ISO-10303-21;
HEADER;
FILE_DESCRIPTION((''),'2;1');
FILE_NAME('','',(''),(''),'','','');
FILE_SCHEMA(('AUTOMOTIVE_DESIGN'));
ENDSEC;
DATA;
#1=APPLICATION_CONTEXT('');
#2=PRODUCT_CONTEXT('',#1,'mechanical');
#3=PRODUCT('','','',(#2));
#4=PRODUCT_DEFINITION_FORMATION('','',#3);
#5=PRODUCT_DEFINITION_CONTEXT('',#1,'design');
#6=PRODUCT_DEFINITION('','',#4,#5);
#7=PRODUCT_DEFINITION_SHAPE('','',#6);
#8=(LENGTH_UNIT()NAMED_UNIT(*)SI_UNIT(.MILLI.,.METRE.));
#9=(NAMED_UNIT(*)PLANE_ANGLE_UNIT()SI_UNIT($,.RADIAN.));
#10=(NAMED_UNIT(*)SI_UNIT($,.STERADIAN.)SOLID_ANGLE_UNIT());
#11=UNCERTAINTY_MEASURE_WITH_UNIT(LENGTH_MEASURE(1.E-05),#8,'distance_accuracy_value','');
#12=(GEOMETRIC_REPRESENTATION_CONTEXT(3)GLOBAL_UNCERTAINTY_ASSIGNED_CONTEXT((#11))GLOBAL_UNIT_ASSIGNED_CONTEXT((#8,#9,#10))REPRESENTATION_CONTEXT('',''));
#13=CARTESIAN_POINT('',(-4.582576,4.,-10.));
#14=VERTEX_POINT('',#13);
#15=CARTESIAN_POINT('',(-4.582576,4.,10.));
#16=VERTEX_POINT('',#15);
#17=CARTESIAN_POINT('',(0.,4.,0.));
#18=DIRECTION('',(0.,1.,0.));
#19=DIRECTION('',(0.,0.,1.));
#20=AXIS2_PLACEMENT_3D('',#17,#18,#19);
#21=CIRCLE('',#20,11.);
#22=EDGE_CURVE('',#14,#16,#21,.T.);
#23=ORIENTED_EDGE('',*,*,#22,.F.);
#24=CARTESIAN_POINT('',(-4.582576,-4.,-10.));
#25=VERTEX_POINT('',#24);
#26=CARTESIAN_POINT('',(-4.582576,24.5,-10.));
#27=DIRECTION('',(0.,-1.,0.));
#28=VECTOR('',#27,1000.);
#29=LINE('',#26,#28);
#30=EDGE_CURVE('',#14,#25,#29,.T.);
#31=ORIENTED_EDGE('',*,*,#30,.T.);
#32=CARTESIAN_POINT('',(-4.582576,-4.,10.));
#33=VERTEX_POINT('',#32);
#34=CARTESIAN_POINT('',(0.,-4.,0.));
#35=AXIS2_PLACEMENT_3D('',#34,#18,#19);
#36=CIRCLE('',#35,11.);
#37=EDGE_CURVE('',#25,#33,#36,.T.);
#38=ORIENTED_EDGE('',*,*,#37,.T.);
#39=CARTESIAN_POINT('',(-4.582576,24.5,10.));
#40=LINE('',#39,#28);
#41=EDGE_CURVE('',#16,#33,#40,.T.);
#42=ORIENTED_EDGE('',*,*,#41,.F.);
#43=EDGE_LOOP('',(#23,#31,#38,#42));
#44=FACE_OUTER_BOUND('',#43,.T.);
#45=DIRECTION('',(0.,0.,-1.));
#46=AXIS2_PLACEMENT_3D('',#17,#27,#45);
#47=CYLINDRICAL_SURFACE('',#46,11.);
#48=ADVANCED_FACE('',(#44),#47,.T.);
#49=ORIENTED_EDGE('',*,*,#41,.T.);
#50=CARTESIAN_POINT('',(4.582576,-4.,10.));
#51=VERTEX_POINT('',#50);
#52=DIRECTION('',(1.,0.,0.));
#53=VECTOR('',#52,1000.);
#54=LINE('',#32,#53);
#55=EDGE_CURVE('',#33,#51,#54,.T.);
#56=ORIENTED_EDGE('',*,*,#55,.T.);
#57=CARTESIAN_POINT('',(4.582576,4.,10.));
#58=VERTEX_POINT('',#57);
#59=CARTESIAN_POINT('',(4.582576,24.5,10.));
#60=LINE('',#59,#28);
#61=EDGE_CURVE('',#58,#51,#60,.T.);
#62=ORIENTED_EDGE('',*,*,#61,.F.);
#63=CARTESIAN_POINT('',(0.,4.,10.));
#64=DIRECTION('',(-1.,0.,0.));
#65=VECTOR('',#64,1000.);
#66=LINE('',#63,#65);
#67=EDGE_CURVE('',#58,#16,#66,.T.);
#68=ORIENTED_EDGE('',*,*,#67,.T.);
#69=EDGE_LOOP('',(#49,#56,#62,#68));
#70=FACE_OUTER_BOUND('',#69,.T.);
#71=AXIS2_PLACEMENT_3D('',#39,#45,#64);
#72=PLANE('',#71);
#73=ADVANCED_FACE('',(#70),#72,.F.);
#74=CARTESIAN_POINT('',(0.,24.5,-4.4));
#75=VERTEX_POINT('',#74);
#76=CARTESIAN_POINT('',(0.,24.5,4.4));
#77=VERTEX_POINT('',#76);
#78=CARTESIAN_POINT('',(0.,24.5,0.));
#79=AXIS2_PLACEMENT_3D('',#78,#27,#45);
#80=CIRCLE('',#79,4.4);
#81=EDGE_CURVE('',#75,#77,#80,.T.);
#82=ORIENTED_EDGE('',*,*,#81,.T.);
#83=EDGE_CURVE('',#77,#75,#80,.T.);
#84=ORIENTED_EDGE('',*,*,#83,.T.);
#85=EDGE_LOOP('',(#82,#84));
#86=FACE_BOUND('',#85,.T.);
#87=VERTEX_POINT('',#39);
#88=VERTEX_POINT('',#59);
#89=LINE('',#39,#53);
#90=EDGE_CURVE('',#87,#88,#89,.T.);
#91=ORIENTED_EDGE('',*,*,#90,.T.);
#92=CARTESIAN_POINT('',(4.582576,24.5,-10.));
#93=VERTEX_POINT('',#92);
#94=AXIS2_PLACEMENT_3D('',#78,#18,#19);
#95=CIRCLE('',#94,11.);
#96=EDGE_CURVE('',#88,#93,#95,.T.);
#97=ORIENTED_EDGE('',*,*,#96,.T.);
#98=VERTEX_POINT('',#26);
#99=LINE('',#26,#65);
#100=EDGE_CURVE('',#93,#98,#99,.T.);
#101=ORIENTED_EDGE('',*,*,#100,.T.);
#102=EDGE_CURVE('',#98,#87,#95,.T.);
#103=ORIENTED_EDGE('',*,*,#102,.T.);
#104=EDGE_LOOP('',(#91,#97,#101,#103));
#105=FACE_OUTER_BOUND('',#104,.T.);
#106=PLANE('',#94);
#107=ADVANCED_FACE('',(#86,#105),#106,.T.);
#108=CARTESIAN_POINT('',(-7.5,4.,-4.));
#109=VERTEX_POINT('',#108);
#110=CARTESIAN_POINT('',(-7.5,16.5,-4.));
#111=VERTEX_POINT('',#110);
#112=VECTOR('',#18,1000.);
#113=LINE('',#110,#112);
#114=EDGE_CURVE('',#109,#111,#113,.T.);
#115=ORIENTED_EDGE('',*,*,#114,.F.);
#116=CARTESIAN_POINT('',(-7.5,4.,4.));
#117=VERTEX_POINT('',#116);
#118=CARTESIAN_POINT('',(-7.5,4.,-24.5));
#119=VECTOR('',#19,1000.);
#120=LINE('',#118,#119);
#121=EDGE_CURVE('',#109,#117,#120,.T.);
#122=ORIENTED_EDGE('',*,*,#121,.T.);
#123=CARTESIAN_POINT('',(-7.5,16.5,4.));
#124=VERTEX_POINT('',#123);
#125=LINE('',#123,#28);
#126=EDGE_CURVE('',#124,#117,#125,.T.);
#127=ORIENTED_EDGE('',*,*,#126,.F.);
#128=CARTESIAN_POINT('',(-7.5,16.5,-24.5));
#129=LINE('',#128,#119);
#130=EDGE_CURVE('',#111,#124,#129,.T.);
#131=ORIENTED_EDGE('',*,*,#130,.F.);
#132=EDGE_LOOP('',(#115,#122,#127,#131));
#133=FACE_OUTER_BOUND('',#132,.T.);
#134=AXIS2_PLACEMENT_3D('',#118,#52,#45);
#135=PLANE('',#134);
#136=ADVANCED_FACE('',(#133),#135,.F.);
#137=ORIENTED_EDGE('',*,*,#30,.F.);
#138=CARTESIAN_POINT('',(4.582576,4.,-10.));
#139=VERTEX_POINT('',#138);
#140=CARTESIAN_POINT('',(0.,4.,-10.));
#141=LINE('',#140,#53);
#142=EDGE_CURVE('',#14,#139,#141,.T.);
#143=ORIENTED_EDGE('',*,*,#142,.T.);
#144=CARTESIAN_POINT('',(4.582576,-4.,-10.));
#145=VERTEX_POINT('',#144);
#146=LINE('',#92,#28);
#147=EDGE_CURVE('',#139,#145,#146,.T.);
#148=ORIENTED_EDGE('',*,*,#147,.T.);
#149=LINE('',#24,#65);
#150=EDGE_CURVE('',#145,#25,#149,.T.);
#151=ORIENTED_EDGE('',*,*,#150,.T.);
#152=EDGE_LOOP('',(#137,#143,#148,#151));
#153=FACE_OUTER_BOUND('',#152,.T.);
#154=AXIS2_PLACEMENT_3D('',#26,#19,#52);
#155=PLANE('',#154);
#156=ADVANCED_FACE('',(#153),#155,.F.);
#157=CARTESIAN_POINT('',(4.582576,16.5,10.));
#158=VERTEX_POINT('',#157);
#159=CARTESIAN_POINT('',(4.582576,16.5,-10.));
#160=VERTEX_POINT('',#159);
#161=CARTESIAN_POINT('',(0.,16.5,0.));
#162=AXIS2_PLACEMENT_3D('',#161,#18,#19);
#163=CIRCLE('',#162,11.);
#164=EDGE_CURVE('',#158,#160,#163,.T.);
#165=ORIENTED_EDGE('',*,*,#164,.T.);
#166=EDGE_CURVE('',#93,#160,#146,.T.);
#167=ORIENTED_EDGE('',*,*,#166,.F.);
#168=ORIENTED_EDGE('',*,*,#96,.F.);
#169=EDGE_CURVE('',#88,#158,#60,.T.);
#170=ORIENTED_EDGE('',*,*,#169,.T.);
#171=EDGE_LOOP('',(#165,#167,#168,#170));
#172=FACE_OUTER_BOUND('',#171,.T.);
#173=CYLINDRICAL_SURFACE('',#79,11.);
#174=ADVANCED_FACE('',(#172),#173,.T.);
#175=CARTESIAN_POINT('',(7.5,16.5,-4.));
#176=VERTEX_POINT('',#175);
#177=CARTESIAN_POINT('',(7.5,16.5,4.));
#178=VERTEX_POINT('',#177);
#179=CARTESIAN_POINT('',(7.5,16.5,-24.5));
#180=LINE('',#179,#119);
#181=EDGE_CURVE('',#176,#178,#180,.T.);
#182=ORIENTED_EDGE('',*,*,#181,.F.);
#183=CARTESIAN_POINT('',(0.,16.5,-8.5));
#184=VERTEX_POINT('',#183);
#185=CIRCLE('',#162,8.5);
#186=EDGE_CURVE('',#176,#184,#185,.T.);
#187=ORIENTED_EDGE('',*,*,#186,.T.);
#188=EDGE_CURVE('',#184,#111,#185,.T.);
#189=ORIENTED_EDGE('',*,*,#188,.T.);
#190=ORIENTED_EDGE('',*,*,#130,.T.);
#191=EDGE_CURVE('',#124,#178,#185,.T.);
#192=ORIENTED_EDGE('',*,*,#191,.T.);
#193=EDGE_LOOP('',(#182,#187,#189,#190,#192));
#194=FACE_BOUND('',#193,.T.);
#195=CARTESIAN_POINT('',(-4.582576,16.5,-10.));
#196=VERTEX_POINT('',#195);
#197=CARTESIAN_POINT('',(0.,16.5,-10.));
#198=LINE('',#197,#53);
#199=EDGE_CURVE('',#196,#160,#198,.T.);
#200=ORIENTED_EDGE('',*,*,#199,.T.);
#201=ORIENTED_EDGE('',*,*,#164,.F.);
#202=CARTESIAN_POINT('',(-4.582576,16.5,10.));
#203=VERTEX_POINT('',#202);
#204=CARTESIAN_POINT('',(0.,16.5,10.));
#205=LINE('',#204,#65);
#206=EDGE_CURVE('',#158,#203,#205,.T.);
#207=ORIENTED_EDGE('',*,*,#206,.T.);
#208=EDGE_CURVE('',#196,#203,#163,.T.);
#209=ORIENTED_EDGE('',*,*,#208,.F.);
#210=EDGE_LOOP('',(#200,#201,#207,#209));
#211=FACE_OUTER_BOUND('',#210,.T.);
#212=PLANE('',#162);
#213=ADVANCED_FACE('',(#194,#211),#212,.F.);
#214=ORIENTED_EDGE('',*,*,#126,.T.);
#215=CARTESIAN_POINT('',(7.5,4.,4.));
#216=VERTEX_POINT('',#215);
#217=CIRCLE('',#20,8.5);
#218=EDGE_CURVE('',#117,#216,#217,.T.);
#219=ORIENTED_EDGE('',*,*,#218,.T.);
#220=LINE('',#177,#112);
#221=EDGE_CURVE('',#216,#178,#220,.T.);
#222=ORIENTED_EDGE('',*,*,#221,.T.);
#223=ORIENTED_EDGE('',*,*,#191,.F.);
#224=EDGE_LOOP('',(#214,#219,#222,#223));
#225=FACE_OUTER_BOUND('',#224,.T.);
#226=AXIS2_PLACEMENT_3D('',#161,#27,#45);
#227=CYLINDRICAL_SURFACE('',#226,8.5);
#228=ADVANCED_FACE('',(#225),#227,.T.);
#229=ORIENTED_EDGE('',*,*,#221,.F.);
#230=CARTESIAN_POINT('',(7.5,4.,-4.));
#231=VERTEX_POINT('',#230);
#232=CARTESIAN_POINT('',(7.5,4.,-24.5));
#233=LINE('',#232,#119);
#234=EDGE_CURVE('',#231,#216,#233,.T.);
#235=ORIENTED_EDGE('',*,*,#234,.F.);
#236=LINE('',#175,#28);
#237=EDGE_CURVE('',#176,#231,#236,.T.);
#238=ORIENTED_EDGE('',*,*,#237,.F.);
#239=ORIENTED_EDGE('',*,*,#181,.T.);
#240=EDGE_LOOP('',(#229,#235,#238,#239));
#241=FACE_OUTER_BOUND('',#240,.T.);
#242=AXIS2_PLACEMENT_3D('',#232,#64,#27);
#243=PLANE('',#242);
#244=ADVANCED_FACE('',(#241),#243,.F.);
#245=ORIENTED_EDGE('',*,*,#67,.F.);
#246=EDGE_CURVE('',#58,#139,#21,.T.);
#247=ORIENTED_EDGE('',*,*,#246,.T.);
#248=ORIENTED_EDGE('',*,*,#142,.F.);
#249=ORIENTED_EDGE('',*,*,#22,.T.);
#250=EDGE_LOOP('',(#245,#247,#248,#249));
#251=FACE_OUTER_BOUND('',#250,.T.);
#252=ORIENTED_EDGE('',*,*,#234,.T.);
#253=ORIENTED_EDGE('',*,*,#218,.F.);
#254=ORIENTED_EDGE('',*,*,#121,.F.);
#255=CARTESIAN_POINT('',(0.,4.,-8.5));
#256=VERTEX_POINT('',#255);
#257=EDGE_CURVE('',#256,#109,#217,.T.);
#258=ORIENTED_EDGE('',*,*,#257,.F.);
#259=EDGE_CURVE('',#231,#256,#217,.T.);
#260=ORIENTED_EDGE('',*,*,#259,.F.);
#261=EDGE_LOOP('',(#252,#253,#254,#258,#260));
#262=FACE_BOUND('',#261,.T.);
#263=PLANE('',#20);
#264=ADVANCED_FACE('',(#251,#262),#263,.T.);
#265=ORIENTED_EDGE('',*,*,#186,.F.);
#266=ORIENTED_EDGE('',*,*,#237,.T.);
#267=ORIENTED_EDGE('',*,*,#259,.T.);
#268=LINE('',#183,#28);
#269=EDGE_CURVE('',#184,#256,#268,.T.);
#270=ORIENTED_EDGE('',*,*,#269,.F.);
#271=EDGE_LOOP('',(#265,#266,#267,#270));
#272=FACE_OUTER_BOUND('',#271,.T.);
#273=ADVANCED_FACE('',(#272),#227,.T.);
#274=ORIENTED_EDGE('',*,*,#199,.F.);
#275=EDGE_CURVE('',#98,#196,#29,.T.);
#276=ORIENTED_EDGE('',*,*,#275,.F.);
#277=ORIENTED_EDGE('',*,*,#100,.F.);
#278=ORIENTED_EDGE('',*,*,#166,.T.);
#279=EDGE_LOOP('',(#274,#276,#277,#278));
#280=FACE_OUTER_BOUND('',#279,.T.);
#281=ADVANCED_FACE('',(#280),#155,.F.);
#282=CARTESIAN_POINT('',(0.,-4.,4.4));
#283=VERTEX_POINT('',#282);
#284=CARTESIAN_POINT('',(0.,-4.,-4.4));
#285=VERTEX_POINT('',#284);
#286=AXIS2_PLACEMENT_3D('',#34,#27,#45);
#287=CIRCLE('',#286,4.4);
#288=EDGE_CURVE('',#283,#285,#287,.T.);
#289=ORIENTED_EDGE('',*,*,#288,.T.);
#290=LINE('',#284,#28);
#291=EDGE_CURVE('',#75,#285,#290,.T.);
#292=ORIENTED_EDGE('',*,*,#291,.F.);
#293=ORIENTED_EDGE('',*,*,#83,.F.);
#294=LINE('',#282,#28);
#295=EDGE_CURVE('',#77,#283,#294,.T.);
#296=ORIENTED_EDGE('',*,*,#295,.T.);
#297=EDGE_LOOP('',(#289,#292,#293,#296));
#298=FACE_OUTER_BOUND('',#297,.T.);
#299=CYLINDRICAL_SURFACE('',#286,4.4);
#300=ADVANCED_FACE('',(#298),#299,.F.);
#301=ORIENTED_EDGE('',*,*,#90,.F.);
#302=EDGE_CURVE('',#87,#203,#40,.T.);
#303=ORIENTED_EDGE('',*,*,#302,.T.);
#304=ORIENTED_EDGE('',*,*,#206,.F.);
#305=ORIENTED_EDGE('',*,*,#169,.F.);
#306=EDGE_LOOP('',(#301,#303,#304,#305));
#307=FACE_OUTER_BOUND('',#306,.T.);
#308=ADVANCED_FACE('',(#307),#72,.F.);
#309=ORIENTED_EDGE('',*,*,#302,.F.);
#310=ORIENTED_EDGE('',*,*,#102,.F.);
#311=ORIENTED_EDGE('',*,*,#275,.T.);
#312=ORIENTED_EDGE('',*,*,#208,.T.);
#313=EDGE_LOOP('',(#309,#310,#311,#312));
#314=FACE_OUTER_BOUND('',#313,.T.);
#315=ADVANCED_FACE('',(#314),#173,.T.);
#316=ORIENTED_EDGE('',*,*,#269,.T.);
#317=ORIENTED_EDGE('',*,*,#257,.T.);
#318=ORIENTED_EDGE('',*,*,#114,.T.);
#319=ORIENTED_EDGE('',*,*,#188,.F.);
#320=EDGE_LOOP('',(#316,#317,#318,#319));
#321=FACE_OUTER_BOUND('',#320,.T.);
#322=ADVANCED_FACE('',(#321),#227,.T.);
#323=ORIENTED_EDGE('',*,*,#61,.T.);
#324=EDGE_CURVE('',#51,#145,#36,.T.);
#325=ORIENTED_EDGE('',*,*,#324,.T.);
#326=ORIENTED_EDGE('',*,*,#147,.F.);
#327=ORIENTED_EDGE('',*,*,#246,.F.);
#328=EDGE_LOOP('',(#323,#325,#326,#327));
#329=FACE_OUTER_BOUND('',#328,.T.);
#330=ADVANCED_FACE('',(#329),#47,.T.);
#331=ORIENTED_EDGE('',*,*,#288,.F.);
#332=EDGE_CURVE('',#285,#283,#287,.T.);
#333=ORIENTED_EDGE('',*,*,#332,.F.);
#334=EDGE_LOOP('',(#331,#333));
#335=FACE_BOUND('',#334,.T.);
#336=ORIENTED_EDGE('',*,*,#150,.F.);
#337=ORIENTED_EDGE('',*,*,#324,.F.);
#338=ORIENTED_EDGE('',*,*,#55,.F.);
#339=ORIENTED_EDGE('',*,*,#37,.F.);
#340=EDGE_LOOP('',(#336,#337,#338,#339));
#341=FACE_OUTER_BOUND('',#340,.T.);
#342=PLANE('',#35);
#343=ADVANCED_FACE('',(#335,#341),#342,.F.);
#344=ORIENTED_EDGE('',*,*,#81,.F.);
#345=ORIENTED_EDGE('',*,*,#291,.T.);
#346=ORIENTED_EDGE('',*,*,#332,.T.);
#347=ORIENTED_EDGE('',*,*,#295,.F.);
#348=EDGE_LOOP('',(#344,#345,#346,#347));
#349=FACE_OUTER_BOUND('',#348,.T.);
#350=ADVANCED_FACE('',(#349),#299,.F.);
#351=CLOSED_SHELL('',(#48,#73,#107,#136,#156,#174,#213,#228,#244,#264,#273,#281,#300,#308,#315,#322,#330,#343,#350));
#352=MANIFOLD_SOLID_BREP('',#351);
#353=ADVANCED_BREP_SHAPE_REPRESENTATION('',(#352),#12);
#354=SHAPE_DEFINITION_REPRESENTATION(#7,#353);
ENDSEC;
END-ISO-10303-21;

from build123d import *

# Parameters (mm, degrees)
SKETCH_1_R          = 11
EXTRUDE_1_DEPTH     = 4
SKETCH_2_R          = 8.5
EXTRUDE_2_DEPTH     = 12.5
EXTRUDE_START       = 8
SKETCH_9_R          = 11
EXTRUDE_3_DEPTH     = 8
M10X1_25_1_D        = 8.8
CUT_EXTRUDE_2_DEPTH = 33.46921619
SKETCH_10_W         = 1
SKETCH_10_H         = 12.5
CUT_EXTRUDE_3_DEPTH = 24.5


with BuildPart() as part:
    # 草图1 → 凸台-拉伸1 (new, symmetric)
    with BuildSketch(Plane(origin=(0, 0, 0), x_dir=(1, 0, 0), z_dir=(0, 1, 0))):
        with Locations(Location((0, 0, 0), (0, 0, 270))):
            Circle(SKETCH_1_R)
    extrude(amount=EXTRUDE_1_DEPTH, both=True)

    # 草图2 → 凸台-拉伸2 (add)
    with BuildSketch(Plane(origin=(0, 4, 0), x_dir=(1, 0, 0), z_dir=(0, 1, 0))):
        with Locations(Location((0, 0, 0), (0, 0, 270))):
            Circle(SKETCH_2_R)
    extrude(amount=EXTRUDE_2_DEPTH)

    # 草图9 → 凸台-拉伸3 (add)
    with BuildSketch(Plane(origin=(0, 16.5, 0), x_dir=(1, 0, 0), z_dir=(0, 1, 0)).offset(EXTRUDE_START)):
        with Locations(Location((0, 0, 0), (0, 0, 270))):
            Circle(SKETCH_9_R)
    extrude(amount=-EXTRUDE_3_DEPTH)

    # M10x1.25 螺纹孔1 (through all)
    with Locations(Plane(origin=(0, -4, 0), x_dir=(-1, 0, 0), z_dir=(0, -1, 0))):
        with Locations((0, 0)):
            Hole(M10X1_25_1_D / 2)

    # 草图6 → 切除-拉伸2 (cut, through all)
    with BuildSketch(Plane.XZ.offset(4)):
        with BuildLine():
            Line((-4.582575695, 10), (4.582575695, 10))
            ThreePointArc((4.582575695, 10), (0, 11), (-4.582575695, 10))
        make_face()
        with BuildLine():
            Line((-4.582575695, -10), (4.582575695, -10))
            ThreePointArc((4.582575695, -10), (0, -11), (-4.582575695, -10))
        make_face()
    extrude(amount=-CUT_EXTRUDE_2_DEPTH, mode=Mode.SUBTRACT)

    # 草图10 → 切除-拉伸3 (cut, symmetric)
    with BuildSketch(Plane.XY):
        with Locations((-8, 10.25)):
            Rectangle(SKETCH_10_W, SKETCH_10_H)
        with Locations((8, 10.25)):
            Rectangle(SKETCH_10_W, SKETCH_10_H)
    extrude(amount=CUT_EXTRUDE_3_DEPTH, both=True, mode=Mode.SUBTRACT)


solid = part.part
